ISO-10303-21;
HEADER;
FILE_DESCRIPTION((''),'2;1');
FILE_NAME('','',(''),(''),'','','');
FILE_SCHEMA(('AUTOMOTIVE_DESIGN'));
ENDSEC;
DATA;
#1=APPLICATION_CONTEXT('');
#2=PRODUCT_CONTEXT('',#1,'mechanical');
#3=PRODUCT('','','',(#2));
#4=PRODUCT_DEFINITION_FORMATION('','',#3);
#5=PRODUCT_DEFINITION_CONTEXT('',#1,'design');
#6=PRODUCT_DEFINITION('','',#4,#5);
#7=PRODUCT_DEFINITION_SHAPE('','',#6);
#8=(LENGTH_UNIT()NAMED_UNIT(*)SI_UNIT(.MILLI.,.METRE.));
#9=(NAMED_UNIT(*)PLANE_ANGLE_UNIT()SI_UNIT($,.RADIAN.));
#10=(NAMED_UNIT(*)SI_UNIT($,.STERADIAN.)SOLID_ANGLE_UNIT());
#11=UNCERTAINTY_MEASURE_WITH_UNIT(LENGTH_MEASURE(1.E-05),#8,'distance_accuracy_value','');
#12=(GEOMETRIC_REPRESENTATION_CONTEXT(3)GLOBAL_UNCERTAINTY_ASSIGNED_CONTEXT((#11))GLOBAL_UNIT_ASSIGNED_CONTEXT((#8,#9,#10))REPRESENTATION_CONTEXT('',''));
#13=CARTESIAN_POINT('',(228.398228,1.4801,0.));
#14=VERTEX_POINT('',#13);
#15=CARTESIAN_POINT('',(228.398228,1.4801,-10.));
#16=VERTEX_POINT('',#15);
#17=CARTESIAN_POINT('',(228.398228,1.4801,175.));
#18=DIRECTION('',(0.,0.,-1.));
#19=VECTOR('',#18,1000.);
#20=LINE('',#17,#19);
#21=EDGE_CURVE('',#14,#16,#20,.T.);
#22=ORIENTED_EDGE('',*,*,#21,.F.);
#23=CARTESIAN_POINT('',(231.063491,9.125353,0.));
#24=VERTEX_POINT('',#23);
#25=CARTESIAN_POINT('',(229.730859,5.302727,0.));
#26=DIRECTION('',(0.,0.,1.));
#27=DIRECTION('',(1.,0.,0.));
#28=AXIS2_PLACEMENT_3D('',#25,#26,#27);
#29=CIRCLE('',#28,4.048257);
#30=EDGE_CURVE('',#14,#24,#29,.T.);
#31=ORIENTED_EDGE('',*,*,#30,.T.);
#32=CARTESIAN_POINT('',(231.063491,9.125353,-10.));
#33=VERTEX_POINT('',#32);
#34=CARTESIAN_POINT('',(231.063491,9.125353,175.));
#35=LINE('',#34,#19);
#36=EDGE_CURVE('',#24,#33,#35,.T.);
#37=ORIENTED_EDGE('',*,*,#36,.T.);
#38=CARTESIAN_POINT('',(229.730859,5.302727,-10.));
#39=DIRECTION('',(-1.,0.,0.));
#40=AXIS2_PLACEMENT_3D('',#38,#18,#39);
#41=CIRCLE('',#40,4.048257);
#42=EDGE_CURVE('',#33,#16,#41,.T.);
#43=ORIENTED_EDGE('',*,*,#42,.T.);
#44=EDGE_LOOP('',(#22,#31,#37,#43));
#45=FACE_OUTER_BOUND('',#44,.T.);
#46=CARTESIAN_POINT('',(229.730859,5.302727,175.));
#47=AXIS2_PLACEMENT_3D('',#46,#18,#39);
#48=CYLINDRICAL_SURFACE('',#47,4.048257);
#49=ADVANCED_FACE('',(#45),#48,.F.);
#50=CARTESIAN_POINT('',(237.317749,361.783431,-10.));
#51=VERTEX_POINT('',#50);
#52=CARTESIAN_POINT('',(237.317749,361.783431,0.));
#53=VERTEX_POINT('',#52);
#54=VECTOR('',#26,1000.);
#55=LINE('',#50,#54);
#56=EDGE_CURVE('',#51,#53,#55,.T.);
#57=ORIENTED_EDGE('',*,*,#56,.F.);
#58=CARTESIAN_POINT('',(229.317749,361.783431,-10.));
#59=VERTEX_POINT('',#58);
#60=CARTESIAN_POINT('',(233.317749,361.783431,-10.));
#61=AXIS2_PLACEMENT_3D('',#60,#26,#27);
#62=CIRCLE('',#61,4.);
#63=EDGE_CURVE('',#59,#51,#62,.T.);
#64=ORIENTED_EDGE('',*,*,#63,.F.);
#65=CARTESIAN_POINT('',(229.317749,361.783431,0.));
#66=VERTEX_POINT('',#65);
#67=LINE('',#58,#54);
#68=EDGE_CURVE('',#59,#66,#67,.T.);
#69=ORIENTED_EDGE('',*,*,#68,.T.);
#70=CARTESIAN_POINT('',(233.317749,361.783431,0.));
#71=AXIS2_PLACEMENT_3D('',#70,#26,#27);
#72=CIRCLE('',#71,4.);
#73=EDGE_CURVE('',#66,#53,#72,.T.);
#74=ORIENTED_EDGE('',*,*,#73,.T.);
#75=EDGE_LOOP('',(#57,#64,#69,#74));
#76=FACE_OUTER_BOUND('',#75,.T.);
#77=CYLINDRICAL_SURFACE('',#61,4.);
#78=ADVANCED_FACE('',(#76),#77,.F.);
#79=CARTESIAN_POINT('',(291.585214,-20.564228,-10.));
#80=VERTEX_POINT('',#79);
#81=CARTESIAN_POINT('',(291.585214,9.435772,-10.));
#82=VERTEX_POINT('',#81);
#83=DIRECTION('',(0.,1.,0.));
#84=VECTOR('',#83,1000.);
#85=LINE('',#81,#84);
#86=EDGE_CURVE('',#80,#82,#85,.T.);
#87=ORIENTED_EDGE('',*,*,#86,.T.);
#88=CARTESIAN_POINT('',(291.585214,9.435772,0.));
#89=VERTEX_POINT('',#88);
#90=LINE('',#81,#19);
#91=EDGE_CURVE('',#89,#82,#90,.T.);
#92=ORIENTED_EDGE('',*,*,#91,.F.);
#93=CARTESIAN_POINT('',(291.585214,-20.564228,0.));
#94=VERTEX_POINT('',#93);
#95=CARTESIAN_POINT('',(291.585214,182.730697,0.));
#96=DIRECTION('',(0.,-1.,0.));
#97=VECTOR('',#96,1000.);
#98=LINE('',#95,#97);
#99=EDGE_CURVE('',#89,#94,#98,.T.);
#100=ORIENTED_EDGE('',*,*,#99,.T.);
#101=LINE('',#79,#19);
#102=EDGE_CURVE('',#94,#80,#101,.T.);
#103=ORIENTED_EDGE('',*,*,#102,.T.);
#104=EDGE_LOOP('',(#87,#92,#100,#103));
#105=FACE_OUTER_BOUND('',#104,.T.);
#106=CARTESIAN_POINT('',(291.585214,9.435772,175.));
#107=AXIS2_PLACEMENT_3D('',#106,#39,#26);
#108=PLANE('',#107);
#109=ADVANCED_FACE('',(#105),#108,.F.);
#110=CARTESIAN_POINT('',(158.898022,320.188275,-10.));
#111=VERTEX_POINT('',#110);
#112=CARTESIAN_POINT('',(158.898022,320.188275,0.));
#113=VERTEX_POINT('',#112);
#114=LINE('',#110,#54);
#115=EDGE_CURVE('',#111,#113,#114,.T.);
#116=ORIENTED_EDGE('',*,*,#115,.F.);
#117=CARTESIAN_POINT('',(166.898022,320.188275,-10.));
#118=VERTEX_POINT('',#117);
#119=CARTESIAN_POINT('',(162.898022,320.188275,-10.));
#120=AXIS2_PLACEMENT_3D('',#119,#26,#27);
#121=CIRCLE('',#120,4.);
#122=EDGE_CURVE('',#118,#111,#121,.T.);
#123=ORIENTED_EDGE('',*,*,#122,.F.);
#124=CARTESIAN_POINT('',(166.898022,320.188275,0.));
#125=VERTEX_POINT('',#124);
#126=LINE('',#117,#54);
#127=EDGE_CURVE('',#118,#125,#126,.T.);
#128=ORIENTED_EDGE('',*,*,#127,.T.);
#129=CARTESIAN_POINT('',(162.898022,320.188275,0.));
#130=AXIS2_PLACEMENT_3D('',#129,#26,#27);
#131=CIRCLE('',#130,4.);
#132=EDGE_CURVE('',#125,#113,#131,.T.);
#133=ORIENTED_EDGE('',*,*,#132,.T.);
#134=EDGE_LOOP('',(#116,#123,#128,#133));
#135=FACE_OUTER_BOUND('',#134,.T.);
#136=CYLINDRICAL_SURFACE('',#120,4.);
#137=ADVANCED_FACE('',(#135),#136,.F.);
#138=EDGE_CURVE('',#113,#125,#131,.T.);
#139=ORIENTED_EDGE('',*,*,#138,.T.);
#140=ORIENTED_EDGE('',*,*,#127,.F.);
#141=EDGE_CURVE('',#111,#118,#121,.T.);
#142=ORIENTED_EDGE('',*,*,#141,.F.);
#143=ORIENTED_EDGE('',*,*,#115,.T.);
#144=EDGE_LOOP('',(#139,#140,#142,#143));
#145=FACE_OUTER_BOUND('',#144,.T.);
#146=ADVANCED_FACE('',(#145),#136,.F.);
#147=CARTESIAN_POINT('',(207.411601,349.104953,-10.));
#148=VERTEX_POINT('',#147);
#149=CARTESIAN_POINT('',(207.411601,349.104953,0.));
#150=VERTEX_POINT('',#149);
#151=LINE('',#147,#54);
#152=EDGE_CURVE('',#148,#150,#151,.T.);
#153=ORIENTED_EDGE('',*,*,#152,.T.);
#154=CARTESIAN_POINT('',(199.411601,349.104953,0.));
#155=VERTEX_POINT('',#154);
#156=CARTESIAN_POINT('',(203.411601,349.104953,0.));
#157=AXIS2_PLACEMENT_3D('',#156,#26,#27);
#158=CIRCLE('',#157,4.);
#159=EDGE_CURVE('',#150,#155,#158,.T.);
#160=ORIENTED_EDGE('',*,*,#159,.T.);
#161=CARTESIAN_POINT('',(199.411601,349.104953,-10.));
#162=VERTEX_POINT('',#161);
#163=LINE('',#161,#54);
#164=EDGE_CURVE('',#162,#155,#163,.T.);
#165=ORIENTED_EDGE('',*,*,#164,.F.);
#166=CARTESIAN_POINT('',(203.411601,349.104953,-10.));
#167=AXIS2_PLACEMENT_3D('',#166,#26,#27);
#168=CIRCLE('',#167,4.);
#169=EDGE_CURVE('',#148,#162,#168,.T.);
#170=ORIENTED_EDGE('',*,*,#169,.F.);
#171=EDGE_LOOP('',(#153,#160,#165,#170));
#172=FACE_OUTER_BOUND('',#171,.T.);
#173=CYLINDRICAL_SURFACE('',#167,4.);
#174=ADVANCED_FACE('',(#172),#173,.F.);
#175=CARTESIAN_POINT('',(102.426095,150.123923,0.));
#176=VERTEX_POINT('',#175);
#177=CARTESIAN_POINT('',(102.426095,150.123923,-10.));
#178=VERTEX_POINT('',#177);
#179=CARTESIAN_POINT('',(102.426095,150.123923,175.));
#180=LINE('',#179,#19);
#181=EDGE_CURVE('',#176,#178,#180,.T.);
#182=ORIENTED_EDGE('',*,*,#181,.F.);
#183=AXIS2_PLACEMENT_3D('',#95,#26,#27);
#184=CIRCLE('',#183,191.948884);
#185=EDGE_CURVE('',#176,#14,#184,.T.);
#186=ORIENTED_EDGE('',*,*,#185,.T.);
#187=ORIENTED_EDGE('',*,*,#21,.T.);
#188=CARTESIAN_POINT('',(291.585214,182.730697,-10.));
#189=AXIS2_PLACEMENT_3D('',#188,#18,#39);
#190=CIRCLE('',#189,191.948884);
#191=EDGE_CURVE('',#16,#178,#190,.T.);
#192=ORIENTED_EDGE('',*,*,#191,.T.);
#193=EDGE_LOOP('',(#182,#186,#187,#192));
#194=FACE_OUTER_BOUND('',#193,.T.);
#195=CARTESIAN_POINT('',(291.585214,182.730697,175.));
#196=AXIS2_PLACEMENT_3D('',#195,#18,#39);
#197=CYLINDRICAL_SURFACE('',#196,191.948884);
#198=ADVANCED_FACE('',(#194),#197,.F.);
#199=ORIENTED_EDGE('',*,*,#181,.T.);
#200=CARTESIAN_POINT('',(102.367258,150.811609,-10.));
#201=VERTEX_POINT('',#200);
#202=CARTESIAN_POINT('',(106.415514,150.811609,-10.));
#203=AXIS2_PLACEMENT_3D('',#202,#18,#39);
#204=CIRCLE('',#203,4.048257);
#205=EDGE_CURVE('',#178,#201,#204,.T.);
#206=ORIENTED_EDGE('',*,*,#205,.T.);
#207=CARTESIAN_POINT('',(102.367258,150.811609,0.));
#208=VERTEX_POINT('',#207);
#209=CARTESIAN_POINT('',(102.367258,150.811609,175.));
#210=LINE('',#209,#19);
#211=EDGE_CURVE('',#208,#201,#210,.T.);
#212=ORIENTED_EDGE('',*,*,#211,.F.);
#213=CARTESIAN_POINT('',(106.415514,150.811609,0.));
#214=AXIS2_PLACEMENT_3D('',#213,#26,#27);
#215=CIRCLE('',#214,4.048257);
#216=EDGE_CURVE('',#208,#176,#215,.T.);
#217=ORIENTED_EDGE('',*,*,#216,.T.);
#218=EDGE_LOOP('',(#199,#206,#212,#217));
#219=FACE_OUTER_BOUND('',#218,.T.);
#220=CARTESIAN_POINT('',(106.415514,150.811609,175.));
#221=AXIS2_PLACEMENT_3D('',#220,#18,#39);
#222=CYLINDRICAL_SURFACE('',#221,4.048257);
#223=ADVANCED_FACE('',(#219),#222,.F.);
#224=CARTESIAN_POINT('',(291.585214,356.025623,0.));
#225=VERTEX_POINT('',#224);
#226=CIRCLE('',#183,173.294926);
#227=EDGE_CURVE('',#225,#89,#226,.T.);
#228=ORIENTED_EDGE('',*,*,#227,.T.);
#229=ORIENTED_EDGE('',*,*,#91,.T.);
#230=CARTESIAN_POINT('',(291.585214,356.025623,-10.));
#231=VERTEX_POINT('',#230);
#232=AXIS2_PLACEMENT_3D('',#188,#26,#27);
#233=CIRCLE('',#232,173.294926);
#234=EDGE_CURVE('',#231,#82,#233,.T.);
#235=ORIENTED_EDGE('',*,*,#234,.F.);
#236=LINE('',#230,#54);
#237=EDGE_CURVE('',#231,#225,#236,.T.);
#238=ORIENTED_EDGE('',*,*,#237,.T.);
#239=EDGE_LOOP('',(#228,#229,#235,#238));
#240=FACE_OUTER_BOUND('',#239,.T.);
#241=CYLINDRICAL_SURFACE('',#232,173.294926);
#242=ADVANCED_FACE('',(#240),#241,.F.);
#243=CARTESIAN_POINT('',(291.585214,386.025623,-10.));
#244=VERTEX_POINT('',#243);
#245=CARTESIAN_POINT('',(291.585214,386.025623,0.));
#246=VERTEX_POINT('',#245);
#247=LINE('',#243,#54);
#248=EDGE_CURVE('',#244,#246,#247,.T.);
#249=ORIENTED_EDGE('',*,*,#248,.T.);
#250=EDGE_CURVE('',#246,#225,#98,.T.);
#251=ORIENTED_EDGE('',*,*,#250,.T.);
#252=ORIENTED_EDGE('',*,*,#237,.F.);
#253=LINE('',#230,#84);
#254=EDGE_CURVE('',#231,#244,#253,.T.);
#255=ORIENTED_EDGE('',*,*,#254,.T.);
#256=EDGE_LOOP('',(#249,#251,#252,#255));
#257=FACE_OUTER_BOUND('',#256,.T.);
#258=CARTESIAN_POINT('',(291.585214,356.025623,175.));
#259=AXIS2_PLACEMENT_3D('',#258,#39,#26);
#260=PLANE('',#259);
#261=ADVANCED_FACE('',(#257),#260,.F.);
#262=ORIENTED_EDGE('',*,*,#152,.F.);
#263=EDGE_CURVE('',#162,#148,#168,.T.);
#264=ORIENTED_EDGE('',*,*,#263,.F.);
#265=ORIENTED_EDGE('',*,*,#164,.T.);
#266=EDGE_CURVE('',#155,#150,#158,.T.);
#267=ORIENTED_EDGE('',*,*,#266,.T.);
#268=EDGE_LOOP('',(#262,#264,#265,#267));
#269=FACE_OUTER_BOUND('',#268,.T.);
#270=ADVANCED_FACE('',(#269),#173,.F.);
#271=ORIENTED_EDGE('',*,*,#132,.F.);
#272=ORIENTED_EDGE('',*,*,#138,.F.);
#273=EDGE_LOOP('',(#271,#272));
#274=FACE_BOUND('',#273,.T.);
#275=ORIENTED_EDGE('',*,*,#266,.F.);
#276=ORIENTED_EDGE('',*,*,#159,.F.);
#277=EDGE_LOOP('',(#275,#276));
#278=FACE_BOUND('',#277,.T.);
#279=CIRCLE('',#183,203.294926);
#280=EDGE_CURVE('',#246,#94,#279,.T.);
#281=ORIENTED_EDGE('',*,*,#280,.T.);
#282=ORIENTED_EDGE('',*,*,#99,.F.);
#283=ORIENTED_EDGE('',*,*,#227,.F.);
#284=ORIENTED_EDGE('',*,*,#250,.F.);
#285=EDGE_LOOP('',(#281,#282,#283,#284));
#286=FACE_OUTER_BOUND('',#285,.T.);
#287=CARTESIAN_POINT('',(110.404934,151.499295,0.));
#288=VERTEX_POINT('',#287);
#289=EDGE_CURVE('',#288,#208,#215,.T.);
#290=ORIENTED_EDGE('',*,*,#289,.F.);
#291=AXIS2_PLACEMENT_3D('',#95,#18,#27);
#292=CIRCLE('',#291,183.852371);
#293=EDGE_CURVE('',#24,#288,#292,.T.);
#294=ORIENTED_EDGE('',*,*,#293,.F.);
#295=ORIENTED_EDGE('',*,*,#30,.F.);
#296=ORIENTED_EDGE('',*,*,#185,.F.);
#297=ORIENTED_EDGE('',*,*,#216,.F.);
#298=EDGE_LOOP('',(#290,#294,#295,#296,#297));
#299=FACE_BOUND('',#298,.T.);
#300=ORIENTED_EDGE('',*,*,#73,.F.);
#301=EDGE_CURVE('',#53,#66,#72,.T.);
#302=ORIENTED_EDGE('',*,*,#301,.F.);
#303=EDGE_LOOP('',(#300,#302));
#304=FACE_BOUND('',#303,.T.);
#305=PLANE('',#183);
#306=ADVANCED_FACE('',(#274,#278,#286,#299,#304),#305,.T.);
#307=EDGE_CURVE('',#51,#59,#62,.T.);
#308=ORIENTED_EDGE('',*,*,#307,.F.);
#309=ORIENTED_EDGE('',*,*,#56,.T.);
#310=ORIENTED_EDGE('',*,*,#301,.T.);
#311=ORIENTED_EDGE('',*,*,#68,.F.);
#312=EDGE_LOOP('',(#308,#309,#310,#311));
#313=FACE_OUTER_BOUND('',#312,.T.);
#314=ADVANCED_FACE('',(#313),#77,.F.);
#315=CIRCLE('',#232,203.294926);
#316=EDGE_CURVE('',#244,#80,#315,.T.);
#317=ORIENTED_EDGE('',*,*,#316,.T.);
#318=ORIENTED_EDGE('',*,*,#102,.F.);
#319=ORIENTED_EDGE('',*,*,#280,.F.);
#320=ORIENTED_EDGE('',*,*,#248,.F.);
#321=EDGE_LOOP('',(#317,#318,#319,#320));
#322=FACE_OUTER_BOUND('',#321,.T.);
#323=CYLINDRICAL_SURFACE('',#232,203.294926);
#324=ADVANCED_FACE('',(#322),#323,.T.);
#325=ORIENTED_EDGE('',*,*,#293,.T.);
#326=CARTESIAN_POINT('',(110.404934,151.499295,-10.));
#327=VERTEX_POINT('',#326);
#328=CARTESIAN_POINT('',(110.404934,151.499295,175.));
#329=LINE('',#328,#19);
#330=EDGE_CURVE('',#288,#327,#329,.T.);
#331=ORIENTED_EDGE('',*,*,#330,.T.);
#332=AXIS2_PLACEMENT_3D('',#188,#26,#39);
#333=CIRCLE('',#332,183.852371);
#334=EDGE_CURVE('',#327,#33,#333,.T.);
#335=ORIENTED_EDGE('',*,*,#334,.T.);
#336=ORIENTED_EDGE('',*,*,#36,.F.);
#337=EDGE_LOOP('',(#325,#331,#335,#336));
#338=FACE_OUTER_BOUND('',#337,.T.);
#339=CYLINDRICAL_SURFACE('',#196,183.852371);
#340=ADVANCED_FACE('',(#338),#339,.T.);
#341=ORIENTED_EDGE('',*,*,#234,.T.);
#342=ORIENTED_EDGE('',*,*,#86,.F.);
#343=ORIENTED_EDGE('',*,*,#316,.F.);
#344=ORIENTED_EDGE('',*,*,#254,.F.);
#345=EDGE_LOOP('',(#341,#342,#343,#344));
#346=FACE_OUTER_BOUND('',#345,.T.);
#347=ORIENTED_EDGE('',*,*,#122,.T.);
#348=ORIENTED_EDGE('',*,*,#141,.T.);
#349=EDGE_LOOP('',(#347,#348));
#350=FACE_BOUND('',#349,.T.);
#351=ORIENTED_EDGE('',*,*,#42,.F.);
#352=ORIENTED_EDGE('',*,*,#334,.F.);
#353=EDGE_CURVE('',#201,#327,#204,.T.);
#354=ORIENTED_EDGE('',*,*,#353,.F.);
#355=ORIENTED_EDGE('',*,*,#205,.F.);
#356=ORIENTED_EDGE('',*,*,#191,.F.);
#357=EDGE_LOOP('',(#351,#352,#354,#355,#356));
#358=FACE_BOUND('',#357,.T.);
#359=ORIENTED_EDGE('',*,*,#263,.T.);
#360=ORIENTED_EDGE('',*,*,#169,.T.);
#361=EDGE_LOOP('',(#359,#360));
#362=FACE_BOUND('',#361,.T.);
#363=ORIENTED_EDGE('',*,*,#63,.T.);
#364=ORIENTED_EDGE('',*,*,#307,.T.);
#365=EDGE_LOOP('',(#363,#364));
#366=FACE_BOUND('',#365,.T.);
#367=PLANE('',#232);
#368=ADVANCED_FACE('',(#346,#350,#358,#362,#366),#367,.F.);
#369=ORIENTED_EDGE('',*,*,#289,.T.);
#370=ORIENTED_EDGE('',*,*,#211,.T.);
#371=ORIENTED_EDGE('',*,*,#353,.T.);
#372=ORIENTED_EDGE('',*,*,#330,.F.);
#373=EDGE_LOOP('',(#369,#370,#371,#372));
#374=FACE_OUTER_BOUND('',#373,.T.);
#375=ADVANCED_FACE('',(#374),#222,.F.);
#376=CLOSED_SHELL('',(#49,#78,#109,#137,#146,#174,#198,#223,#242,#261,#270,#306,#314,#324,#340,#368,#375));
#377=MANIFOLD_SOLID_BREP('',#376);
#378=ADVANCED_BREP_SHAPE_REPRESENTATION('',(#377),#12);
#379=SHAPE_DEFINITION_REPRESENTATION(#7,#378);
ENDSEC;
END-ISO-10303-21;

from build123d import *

# Parameters (mm, degrees)
SKETCH1_R               = 203.294925519
SKETCH1_R_2             = 173.294925519
BOSS_EXTRUDE1_DEPTH     = 10
CUT_EXTRUDE1_START      = -185
CUT_EXTRUDE1_DEPTH      = 185
CUT_EXTRUDE2_DEPTH      = 185
CUT_EXTRUDE3_DEPTH      = 484.877792972
CUT_EXTRUDE3_DEPTH_BACK = 484.877792972
SKETCH5_R               = 4


with BuildPart() as part:
    # Sketch1 → Boss-Extrude1 (new body)
    with BuildSketch(Plane.XY):
        with Locations((291.585214163, 182.730697222)):
            Circle(SKETCH1_R)
        with Locations((291.585214163, 182.730697222)):
            Circle(SKETCH1_R_2, mode=Mode.SUBTRACT)
    extrude(amount=-BOSS_EXTRUDE1_DEPTH)

    # Sketch2 → Cut-Extrude1 (cut)
    with BuildSketch(Plane(origin=(0, 0, -10), x_dir=(-1, 0, 0), z_dir=(0, 0, -1)).offset(CUT_EXTRUDE1_START)):
        with BuildLine():
            Line((-291.585214163, 9.435771703), (-291.585214163, -33.905509081))
            ThreePointArc((-291.585214163, -33.905509081), (-508.221420466, 182.730697222), (-291.585214163, 399.366903525))
            Line((-291.585214163, 399.366903525), (-291.585214163, 356.025622742))
            ThreePointArc((-291.585214163, 356.025622742), (-464.880139683, 182.730697222), (-291.585214163, 9.435771703))
        make_face()
    extrude(amount=CUT_EXTRUDE1_DEPTH, mode=Mode.SUBTRACT)

    # Sketch3 → Cut-Extrude2 (cut)
    with BuildSketch(Plane(origin=(0, 0, -10), x_dir=(-1, 0, 0), z_dir=(0, 0, -1))):
        with BuildLine():
            ThreePointArc((-228.398227799, 1.480100191), (-145.149611461, 58.629978323), (-102.426094867, 150.123922508))
            ThreePointArc((-102.426094867, 150.123922508), (-105.727828311, 154.801028245), (-110.404934048, 151.499294801))
            ThreePointArc((-110.404934048, 151.499294801), (-151.326348425, 63.864617192), (-231.063490803, 9.125353407))
            ThreePointArc((-231.063490803, 9.125353407), (-233.553485909, 3.970095297), (-228.398227799, 1.480100191))
        make_face()
    extrude(amount=-CUT_EXTRUDE2_DEPTH, mode=Mode.SUBTRACT)

    # Sketch5 → Cut-Extrude3 (cut, two sides: drawn at the far end of the back side and taken through both)
    with BuildSketch(Plane.XY.offset(-CUT_EXTRUDE3_DEPTH_BACK)):
        with Locations((233.317748738, 361.783430933)):
            Circle(SKETCH5_R)
        with Locations((203.411601384, 349.104953001)):
            Circle(SKETCH5_R)
        with Locations((162.898022452, 320.188274917)):
            Circle(SKETCH5_R)
    extrude(amount=CUT_EXTRUDE3_DEPTH + CUT_EXTRUDE3_DEPTH_BACK, mode=Mode.SUBTRACT)


solid = part.part
